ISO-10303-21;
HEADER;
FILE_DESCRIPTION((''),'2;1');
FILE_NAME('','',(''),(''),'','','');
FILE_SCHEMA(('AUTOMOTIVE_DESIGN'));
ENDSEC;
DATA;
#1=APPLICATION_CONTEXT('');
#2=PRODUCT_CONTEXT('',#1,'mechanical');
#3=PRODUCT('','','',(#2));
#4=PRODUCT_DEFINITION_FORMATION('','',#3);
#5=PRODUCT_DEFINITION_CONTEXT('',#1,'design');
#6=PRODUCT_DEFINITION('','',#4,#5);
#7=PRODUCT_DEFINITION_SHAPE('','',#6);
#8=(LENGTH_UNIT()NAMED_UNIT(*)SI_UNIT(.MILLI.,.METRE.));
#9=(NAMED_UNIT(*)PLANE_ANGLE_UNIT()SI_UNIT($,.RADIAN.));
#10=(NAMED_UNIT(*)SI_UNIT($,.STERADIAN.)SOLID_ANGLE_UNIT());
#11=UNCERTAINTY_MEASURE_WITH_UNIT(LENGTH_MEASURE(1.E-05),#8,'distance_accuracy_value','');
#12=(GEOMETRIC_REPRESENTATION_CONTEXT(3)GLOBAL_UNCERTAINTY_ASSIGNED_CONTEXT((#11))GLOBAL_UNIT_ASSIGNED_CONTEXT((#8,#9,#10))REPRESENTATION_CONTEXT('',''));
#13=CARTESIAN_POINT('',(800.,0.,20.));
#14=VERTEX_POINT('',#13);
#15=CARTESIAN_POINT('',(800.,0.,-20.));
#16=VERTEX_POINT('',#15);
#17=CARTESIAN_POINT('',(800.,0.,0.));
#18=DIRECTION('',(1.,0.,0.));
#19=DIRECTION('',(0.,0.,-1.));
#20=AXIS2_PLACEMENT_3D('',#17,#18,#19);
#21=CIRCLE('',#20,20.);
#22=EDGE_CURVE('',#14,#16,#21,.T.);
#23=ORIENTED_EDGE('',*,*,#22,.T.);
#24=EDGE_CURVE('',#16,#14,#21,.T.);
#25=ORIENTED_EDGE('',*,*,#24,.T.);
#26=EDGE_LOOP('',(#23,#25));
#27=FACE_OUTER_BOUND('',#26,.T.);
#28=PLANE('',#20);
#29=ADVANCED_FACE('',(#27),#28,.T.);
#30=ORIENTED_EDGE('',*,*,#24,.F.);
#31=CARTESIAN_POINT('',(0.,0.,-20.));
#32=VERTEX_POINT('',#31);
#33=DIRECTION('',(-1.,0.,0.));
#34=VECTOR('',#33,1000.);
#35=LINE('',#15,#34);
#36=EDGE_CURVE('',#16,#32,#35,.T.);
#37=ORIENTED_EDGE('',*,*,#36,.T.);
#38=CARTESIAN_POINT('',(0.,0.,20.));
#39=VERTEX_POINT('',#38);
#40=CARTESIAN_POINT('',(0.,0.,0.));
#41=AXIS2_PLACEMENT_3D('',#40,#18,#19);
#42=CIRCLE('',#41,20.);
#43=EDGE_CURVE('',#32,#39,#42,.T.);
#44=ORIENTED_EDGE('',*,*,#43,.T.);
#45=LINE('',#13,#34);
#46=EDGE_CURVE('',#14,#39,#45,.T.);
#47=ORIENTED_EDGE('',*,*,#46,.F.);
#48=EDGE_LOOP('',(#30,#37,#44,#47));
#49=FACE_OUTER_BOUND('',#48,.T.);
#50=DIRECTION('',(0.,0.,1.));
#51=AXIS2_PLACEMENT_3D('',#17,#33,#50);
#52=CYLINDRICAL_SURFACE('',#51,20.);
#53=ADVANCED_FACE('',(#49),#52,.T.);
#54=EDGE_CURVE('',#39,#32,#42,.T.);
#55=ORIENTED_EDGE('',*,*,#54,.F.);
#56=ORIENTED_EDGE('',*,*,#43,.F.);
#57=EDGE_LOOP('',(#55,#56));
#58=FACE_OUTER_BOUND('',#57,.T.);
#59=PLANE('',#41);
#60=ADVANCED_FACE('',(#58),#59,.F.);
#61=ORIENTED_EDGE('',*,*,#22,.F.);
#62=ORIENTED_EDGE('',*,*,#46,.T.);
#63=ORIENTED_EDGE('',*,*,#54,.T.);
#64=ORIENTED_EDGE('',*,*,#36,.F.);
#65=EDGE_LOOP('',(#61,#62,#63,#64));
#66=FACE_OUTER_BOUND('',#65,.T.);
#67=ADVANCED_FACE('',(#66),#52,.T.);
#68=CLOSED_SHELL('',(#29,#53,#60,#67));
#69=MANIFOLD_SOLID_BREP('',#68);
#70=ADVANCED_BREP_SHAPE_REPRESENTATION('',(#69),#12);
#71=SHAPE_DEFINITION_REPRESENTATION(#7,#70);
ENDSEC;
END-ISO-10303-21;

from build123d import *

# Parameters (mm, degrees)
SKETCH1_R    = 20
LENGTH_DEPTH = 800


with BuildPart() as part:
    # Sketch1 → Length (new body)
    with BuildSketch(Plane(origin=(0, 0, 0), x_dir=(0, 0, -1), z_dir=(1, 0, 0))):
        Circle(SKETCH1_R)
    extrude(amount=LENGTH_DEPTH)


solid = part.part
